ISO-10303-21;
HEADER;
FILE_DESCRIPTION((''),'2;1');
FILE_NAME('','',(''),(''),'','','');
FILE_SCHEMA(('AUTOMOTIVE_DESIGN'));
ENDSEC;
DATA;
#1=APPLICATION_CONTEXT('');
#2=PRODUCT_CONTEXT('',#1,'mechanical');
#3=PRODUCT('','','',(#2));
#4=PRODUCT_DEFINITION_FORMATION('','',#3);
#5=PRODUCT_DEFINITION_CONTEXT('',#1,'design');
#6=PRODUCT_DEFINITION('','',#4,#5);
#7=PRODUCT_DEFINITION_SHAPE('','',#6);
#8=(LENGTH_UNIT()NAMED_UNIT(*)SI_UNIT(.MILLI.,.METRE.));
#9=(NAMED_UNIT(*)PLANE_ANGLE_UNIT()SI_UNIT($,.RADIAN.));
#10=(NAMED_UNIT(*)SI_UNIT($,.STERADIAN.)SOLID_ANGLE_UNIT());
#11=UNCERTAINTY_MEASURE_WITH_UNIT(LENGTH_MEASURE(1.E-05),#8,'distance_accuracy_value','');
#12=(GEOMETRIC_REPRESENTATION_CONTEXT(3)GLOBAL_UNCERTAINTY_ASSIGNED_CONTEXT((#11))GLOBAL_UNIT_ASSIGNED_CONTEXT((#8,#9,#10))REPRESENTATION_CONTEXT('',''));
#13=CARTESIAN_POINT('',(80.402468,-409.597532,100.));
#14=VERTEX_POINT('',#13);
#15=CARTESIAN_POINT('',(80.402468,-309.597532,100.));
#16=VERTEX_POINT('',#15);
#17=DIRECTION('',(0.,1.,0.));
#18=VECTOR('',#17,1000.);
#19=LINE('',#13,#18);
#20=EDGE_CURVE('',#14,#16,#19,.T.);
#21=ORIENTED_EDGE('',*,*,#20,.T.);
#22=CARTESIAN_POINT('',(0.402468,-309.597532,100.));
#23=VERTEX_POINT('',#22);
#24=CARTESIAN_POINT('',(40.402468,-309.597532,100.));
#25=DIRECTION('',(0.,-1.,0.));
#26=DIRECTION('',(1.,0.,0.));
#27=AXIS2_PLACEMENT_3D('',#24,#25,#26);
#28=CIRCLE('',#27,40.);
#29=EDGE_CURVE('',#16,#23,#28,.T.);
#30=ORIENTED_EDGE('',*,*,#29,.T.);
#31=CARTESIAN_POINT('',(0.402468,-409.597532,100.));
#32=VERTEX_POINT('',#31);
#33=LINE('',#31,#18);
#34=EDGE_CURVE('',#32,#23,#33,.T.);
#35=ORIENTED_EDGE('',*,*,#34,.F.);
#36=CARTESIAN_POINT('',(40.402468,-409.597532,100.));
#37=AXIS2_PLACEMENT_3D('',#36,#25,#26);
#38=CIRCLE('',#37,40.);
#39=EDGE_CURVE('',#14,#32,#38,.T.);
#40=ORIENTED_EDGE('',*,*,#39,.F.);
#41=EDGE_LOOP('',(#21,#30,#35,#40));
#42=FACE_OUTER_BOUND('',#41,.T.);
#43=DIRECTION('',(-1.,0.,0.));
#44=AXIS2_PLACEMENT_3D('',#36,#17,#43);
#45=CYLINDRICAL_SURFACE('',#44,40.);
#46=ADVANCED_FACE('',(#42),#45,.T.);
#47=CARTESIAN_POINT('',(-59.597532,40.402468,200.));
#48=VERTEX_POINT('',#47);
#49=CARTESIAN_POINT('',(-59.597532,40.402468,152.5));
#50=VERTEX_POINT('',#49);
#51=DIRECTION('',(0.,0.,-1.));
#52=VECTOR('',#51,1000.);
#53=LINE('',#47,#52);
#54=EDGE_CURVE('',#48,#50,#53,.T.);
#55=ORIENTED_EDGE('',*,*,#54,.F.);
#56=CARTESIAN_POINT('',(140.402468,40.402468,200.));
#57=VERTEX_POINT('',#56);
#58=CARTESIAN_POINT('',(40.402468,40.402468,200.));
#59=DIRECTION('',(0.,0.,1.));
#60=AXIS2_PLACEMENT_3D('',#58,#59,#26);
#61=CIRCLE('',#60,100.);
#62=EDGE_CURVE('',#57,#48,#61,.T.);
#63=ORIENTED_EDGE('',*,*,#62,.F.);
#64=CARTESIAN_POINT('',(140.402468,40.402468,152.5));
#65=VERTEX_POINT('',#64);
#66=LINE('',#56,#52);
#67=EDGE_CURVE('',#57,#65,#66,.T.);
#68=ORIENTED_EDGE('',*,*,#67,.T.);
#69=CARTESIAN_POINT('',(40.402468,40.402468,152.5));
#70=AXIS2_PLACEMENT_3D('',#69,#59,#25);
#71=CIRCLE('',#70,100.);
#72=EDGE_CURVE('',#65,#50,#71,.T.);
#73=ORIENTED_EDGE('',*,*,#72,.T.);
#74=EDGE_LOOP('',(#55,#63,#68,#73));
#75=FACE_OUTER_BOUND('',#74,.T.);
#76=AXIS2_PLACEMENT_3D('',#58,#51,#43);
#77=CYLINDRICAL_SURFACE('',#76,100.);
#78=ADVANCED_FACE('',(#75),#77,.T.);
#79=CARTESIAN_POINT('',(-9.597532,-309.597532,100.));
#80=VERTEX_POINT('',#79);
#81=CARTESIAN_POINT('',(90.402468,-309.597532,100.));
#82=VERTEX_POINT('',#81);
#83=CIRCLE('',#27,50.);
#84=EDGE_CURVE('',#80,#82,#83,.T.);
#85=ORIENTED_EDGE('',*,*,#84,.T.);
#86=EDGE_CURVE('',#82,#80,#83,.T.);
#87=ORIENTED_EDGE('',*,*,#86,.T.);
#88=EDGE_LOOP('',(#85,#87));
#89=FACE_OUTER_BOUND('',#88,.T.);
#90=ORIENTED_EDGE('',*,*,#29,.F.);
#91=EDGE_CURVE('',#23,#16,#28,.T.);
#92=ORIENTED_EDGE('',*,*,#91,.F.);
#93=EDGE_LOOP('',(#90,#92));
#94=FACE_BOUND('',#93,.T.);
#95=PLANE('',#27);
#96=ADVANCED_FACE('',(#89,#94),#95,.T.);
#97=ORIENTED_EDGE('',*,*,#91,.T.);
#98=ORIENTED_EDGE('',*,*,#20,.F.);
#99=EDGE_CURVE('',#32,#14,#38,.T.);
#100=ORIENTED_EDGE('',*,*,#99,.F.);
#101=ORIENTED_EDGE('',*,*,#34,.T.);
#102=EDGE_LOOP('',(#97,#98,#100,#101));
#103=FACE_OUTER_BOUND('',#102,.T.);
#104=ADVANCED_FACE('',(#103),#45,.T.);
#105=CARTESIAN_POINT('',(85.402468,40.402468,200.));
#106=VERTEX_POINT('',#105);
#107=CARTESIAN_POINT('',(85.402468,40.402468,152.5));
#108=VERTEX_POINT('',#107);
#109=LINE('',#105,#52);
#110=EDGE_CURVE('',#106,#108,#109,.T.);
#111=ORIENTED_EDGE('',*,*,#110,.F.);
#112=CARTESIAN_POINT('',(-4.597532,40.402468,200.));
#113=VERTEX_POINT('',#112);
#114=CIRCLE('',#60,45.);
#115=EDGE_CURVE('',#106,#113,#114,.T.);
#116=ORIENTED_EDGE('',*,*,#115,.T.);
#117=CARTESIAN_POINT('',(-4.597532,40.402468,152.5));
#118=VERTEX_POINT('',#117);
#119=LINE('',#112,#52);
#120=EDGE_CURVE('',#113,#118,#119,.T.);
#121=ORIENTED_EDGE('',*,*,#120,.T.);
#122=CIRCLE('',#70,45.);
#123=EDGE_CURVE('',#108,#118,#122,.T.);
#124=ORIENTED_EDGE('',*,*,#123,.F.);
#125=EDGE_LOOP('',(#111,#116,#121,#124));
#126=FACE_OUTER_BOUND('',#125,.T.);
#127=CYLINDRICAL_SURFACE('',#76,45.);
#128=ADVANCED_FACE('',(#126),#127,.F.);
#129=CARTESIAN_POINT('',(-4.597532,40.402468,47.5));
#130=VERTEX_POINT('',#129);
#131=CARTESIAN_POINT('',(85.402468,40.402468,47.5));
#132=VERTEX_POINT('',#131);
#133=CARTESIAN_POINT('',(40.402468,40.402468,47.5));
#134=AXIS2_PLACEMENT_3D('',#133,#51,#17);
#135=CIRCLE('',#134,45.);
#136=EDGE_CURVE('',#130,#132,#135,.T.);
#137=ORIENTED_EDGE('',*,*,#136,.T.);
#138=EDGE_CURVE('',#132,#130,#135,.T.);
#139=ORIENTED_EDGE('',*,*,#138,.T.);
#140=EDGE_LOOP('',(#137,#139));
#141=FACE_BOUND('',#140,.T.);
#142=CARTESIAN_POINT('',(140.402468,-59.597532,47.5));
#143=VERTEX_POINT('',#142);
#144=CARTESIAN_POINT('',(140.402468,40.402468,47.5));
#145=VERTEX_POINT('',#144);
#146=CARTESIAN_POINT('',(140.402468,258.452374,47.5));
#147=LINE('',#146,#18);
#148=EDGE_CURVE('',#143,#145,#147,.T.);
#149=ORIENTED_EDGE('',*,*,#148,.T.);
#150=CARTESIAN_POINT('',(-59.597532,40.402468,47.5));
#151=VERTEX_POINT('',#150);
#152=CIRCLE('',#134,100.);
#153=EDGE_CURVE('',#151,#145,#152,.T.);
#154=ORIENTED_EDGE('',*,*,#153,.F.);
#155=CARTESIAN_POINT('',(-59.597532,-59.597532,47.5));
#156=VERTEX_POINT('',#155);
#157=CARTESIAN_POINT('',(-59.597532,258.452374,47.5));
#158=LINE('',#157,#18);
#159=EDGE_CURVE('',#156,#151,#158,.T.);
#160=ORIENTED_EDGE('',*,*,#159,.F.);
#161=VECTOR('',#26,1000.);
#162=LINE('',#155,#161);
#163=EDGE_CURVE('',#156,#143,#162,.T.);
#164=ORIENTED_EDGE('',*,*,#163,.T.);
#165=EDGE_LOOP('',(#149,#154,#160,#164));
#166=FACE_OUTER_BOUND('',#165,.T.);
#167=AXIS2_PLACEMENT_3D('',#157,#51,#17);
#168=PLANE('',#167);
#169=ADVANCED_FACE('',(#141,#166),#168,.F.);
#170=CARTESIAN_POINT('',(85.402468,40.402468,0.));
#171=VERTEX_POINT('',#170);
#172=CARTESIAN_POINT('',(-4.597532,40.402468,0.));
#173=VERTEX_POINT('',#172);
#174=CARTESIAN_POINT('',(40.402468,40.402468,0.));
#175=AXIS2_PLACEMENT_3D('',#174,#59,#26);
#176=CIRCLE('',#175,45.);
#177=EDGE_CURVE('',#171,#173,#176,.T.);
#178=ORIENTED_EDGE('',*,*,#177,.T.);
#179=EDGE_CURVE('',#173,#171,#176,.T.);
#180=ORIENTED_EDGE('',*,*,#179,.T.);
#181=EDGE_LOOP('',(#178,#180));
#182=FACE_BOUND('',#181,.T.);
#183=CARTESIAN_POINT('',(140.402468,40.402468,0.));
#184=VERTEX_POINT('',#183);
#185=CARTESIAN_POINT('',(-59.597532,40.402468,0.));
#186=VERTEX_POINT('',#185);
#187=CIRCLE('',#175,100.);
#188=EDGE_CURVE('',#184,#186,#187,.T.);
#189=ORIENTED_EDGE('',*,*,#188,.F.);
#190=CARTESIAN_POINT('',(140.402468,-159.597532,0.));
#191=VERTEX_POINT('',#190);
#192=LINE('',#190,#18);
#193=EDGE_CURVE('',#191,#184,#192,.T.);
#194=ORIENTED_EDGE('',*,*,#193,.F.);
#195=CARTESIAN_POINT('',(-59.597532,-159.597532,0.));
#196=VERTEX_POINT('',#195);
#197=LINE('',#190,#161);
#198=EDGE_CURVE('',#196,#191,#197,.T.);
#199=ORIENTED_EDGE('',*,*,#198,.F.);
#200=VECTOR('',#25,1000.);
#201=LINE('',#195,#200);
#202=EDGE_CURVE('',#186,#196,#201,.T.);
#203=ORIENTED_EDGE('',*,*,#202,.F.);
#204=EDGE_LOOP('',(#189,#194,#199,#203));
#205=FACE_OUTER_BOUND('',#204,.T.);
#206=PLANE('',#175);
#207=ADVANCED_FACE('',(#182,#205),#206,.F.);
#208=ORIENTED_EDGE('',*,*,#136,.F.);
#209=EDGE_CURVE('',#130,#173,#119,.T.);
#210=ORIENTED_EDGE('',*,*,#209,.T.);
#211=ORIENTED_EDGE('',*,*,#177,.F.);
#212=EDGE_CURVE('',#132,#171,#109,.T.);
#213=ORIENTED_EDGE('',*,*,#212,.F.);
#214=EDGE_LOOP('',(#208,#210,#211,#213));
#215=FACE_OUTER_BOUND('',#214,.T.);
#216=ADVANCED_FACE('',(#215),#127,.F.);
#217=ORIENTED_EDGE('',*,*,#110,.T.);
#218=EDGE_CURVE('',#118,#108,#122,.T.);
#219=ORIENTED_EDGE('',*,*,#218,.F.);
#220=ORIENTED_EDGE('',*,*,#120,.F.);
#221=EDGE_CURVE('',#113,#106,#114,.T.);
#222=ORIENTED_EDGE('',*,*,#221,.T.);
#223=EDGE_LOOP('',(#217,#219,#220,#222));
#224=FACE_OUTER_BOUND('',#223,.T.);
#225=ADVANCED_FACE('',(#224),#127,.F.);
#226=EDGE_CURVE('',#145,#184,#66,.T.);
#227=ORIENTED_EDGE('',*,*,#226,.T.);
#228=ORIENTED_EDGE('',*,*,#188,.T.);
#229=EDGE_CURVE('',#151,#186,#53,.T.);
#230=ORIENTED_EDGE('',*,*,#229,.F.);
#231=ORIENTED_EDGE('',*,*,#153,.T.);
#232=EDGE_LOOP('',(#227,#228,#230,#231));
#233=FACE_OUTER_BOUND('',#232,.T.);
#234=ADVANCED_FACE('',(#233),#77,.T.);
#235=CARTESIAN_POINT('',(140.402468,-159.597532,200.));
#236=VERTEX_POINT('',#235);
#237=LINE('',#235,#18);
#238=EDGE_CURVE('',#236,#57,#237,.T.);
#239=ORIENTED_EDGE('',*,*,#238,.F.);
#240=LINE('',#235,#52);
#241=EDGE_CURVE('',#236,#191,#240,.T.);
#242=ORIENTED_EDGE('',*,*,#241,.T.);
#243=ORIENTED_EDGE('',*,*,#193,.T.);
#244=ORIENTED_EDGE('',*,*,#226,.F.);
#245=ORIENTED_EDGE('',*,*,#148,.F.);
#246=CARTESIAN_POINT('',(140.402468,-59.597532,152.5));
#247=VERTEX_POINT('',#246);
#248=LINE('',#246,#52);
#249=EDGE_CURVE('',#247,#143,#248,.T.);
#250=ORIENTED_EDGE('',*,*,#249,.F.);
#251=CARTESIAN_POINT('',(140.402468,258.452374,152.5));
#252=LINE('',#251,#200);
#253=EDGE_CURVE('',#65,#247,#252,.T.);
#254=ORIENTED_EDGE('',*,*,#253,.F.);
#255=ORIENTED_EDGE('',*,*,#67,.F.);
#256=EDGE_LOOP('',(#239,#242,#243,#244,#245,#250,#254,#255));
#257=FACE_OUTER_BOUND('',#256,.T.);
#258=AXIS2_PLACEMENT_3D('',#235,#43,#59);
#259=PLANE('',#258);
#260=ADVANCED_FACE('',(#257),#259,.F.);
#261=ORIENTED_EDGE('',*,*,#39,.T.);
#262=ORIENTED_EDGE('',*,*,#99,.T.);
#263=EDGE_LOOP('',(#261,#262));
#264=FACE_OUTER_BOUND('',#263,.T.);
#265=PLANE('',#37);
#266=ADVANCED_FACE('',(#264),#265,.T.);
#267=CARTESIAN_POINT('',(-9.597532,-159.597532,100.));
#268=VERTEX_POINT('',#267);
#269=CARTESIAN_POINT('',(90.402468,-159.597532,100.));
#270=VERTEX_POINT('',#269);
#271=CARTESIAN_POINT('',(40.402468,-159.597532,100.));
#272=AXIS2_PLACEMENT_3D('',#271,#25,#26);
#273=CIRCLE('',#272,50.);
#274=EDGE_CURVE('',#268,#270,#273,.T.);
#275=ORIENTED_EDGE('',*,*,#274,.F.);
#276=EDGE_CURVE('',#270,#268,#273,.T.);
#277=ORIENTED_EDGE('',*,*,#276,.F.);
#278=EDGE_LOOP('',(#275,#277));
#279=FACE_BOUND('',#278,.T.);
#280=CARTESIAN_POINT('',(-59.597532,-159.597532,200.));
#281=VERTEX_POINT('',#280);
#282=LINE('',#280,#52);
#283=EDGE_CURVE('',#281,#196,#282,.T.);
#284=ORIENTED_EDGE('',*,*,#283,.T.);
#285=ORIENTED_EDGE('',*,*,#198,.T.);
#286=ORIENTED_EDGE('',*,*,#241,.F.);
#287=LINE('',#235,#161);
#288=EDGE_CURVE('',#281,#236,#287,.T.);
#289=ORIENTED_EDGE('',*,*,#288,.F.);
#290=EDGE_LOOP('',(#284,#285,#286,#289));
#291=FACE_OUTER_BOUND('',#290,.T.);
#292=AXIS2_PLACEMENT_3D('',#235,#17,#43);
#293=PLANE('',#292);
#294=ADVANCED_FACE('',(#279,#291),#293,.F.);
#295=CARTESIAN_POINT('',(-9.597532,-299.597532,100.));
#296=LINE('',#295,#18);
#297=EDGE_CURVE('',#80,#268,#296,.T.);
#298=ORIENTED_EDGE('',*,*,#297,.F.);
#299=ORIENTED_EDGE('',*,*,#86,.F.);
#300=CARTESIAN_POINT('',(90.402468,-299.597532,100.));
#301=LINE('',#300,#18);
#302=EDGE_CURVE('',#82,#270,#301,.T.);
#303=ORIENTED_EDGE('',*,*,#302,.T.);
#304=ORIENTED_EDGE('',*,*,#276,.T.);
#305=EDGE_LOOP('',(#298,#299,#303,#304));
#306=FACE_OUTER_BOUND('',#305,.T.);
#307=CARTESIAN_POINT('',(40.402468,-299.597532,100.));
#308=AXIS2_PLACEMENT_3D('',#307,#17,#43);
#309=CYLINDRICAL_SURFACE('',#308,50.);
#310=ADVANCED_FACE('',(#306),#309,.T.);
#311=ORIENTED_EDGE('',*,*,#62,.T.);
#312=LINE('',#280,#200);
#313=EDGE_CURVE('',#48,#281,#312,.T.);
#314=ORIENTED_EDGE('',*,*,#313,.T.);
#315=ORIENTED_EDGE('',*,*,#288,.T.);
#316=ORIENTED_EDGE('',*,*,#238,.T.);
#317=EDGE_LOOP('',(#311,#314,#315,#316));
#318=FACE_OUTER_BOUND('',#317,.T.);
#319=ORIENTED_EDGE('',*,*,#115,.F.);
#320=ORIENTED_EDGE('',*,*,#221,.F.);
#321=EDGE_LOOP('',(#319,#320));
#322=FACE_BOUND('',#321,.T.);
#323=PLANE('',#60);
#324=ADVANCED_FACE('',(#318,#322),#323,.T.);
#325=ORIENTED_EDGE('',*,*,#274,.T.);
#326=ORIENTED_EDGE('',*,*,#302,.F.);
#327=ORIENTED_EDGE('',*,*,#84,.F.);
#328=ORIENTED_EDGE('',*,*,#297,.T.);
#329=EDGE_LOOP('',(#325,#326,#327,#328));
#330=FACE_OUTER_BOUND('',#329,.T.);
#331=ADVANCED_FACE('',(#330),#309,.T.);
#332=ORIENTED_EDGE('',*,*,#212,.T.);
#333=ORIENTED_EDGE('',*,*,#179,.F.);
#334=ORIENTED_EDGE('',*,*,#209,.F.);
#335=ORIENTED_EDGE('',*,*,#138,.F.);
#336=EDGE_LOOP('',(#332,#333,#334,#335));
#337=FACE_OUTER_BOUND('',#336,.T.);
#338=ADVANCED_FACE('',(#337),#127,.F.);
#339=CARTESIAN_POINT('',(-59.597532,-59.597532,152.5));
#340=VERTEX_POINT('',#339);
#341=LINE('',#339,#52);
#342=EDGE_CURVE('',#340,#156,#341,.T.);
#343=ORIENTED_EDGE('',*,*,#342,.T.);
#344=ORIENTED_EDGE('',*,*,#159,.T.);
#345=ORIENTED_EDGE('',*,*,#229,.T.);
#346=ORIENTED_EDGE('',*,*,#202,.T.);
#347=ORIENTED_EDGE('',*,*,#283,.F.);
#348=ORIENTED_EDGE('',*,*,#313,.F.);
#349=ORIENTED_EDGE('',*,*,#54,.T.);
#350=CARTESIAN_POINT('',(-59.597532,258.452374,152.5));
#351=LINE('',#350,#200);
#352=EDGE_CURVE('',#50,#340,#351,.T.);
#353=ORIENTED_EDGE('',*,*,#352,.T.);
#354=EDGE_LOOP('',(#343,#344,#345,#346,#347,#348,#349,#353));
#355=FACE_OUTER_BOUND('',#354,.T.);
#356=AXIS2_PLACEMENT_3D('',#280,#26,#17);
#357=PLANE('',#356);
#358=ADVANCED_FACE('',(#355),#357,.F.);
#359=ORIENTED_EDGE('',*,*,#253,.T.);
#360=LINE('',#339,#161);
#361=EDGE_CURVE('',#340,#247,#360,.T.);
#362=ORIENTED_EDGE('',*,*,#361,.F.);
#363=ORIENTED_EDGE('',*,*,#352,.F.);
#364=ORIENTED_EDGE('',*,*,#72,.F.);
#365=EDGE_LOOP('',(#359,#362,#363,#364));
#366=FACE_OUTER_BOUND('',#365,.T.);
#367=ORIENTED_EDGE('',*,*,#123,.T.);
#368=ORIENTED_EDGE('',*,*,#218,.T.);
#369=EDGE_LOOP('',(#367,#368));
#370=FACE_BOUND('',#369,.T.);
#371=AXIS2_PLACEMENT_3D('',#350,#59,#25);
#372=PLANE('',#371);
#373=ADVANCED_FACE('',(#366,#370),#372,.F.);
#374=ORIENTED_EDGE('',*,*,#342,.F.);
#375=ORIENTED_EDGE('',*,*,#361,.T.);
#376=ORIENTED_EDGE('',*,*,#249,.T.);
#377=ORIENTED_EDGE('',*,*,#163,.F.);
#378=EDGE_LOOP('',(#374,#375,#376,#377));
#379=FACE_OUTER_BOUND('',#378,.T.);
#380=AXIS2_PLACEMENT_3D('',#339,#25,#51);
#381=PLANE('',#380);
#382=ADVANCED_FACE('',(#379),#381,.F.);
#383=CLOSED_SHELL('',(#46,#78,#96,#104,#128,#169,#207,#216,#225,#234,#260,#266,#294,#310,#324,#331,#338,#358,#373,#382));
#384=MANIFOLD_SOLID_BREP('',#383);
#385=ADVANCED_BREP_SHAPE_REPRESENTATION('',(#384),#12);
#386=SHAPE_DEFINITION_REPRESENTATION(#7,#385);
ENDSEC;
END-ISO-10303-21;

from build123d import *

# Parameters (mm, degrees)
SKETCH1_R           = 45
BOSS_EXTRUDE2_DEPTH = 200
SKETCH2_W           = 105
SKETCH2_H           = 318.049906591
CUT_EXTRUDE1_DEPTH  = 325.763563649
SKETCH3_R           = 50
BOSS_EXTRUDE3_DEPTH = 140
SKETCH4_R           = 50
BOSS_EXTRUDE4_DEPTH = 10
SKETCH5_R           = 40
BOSS_EXTRUDE5_DEPTH = 100


with BuildPart() as part:
    # Sketch1 → Boss-Extrude2 (new body)
    with BuildSketch(Plane.XY):
        with BuildLine():
            Line((140.402467833, -159.597532167), (-59.597532167, -159.597532167))
            Line((-59.597532167, -159.597532167), (-59.597532167, 40.402467833))
            ThreePointArc((-59.597532167, 40.402467833), (40.402467833, 140.402467833), (140.402467833, 40.402467833))
            Line((140.402467833, 40.402467833), (140.402467833, -159.597532167))
        make_face()
        with Locations((40.402467833, 40.402467833)):
            Circle(SKETCH1_R, mode=Mode.SUBTRACT)
    extrude(amount=BOSS_EXTRUDE2_DEPTH)

    # Sketch2 → Cut-Extrude1 (cut, through all)
    with BuildSketch(Plane(origin=(140.402467833, 0, 0), x_dir=(0, 0, -1), z_dir=(1, 0, 0))):
        with Locations((-100, 99.427421129)):
            Rectangle(SKETCH2_W, SKETCH2_H)
    extrude(amount=-CUT_EXTRUDE1_DEPTH, mode=Mode.SUBTRACT)

    # Sketch3 → Boss-Extrude3 (add)
    with BuildSketch(Plane.XZ.offset(159.597532167)):
        with Locations((40.402467833, 100)):
            Circle(SKETCH3_R)
    extrude(amount=BOSS_EXTRUDE3_DEPTH)

    # Sketch4 → Boss-Extrude4 (add)
    with BuildSketch(Plane.XZ.offset(299.597532167)):
        with Locations((40.402467833, 100)):
            Circle(SKETCH4_R)
    extrude(amount=BOSS_EXTRUDE4_DEPTH)

    # Sketch5 → Boss-Extrude5 (add)
    with BuildSketch(Plane.XZ.offset(309.597532167)):
        with Locations((40.402467833, 100)):
            Circle(SKETCH5_R)
    extrude(amount=BOSS_EXTRUDE5_DEPTH)


solid = part.part
